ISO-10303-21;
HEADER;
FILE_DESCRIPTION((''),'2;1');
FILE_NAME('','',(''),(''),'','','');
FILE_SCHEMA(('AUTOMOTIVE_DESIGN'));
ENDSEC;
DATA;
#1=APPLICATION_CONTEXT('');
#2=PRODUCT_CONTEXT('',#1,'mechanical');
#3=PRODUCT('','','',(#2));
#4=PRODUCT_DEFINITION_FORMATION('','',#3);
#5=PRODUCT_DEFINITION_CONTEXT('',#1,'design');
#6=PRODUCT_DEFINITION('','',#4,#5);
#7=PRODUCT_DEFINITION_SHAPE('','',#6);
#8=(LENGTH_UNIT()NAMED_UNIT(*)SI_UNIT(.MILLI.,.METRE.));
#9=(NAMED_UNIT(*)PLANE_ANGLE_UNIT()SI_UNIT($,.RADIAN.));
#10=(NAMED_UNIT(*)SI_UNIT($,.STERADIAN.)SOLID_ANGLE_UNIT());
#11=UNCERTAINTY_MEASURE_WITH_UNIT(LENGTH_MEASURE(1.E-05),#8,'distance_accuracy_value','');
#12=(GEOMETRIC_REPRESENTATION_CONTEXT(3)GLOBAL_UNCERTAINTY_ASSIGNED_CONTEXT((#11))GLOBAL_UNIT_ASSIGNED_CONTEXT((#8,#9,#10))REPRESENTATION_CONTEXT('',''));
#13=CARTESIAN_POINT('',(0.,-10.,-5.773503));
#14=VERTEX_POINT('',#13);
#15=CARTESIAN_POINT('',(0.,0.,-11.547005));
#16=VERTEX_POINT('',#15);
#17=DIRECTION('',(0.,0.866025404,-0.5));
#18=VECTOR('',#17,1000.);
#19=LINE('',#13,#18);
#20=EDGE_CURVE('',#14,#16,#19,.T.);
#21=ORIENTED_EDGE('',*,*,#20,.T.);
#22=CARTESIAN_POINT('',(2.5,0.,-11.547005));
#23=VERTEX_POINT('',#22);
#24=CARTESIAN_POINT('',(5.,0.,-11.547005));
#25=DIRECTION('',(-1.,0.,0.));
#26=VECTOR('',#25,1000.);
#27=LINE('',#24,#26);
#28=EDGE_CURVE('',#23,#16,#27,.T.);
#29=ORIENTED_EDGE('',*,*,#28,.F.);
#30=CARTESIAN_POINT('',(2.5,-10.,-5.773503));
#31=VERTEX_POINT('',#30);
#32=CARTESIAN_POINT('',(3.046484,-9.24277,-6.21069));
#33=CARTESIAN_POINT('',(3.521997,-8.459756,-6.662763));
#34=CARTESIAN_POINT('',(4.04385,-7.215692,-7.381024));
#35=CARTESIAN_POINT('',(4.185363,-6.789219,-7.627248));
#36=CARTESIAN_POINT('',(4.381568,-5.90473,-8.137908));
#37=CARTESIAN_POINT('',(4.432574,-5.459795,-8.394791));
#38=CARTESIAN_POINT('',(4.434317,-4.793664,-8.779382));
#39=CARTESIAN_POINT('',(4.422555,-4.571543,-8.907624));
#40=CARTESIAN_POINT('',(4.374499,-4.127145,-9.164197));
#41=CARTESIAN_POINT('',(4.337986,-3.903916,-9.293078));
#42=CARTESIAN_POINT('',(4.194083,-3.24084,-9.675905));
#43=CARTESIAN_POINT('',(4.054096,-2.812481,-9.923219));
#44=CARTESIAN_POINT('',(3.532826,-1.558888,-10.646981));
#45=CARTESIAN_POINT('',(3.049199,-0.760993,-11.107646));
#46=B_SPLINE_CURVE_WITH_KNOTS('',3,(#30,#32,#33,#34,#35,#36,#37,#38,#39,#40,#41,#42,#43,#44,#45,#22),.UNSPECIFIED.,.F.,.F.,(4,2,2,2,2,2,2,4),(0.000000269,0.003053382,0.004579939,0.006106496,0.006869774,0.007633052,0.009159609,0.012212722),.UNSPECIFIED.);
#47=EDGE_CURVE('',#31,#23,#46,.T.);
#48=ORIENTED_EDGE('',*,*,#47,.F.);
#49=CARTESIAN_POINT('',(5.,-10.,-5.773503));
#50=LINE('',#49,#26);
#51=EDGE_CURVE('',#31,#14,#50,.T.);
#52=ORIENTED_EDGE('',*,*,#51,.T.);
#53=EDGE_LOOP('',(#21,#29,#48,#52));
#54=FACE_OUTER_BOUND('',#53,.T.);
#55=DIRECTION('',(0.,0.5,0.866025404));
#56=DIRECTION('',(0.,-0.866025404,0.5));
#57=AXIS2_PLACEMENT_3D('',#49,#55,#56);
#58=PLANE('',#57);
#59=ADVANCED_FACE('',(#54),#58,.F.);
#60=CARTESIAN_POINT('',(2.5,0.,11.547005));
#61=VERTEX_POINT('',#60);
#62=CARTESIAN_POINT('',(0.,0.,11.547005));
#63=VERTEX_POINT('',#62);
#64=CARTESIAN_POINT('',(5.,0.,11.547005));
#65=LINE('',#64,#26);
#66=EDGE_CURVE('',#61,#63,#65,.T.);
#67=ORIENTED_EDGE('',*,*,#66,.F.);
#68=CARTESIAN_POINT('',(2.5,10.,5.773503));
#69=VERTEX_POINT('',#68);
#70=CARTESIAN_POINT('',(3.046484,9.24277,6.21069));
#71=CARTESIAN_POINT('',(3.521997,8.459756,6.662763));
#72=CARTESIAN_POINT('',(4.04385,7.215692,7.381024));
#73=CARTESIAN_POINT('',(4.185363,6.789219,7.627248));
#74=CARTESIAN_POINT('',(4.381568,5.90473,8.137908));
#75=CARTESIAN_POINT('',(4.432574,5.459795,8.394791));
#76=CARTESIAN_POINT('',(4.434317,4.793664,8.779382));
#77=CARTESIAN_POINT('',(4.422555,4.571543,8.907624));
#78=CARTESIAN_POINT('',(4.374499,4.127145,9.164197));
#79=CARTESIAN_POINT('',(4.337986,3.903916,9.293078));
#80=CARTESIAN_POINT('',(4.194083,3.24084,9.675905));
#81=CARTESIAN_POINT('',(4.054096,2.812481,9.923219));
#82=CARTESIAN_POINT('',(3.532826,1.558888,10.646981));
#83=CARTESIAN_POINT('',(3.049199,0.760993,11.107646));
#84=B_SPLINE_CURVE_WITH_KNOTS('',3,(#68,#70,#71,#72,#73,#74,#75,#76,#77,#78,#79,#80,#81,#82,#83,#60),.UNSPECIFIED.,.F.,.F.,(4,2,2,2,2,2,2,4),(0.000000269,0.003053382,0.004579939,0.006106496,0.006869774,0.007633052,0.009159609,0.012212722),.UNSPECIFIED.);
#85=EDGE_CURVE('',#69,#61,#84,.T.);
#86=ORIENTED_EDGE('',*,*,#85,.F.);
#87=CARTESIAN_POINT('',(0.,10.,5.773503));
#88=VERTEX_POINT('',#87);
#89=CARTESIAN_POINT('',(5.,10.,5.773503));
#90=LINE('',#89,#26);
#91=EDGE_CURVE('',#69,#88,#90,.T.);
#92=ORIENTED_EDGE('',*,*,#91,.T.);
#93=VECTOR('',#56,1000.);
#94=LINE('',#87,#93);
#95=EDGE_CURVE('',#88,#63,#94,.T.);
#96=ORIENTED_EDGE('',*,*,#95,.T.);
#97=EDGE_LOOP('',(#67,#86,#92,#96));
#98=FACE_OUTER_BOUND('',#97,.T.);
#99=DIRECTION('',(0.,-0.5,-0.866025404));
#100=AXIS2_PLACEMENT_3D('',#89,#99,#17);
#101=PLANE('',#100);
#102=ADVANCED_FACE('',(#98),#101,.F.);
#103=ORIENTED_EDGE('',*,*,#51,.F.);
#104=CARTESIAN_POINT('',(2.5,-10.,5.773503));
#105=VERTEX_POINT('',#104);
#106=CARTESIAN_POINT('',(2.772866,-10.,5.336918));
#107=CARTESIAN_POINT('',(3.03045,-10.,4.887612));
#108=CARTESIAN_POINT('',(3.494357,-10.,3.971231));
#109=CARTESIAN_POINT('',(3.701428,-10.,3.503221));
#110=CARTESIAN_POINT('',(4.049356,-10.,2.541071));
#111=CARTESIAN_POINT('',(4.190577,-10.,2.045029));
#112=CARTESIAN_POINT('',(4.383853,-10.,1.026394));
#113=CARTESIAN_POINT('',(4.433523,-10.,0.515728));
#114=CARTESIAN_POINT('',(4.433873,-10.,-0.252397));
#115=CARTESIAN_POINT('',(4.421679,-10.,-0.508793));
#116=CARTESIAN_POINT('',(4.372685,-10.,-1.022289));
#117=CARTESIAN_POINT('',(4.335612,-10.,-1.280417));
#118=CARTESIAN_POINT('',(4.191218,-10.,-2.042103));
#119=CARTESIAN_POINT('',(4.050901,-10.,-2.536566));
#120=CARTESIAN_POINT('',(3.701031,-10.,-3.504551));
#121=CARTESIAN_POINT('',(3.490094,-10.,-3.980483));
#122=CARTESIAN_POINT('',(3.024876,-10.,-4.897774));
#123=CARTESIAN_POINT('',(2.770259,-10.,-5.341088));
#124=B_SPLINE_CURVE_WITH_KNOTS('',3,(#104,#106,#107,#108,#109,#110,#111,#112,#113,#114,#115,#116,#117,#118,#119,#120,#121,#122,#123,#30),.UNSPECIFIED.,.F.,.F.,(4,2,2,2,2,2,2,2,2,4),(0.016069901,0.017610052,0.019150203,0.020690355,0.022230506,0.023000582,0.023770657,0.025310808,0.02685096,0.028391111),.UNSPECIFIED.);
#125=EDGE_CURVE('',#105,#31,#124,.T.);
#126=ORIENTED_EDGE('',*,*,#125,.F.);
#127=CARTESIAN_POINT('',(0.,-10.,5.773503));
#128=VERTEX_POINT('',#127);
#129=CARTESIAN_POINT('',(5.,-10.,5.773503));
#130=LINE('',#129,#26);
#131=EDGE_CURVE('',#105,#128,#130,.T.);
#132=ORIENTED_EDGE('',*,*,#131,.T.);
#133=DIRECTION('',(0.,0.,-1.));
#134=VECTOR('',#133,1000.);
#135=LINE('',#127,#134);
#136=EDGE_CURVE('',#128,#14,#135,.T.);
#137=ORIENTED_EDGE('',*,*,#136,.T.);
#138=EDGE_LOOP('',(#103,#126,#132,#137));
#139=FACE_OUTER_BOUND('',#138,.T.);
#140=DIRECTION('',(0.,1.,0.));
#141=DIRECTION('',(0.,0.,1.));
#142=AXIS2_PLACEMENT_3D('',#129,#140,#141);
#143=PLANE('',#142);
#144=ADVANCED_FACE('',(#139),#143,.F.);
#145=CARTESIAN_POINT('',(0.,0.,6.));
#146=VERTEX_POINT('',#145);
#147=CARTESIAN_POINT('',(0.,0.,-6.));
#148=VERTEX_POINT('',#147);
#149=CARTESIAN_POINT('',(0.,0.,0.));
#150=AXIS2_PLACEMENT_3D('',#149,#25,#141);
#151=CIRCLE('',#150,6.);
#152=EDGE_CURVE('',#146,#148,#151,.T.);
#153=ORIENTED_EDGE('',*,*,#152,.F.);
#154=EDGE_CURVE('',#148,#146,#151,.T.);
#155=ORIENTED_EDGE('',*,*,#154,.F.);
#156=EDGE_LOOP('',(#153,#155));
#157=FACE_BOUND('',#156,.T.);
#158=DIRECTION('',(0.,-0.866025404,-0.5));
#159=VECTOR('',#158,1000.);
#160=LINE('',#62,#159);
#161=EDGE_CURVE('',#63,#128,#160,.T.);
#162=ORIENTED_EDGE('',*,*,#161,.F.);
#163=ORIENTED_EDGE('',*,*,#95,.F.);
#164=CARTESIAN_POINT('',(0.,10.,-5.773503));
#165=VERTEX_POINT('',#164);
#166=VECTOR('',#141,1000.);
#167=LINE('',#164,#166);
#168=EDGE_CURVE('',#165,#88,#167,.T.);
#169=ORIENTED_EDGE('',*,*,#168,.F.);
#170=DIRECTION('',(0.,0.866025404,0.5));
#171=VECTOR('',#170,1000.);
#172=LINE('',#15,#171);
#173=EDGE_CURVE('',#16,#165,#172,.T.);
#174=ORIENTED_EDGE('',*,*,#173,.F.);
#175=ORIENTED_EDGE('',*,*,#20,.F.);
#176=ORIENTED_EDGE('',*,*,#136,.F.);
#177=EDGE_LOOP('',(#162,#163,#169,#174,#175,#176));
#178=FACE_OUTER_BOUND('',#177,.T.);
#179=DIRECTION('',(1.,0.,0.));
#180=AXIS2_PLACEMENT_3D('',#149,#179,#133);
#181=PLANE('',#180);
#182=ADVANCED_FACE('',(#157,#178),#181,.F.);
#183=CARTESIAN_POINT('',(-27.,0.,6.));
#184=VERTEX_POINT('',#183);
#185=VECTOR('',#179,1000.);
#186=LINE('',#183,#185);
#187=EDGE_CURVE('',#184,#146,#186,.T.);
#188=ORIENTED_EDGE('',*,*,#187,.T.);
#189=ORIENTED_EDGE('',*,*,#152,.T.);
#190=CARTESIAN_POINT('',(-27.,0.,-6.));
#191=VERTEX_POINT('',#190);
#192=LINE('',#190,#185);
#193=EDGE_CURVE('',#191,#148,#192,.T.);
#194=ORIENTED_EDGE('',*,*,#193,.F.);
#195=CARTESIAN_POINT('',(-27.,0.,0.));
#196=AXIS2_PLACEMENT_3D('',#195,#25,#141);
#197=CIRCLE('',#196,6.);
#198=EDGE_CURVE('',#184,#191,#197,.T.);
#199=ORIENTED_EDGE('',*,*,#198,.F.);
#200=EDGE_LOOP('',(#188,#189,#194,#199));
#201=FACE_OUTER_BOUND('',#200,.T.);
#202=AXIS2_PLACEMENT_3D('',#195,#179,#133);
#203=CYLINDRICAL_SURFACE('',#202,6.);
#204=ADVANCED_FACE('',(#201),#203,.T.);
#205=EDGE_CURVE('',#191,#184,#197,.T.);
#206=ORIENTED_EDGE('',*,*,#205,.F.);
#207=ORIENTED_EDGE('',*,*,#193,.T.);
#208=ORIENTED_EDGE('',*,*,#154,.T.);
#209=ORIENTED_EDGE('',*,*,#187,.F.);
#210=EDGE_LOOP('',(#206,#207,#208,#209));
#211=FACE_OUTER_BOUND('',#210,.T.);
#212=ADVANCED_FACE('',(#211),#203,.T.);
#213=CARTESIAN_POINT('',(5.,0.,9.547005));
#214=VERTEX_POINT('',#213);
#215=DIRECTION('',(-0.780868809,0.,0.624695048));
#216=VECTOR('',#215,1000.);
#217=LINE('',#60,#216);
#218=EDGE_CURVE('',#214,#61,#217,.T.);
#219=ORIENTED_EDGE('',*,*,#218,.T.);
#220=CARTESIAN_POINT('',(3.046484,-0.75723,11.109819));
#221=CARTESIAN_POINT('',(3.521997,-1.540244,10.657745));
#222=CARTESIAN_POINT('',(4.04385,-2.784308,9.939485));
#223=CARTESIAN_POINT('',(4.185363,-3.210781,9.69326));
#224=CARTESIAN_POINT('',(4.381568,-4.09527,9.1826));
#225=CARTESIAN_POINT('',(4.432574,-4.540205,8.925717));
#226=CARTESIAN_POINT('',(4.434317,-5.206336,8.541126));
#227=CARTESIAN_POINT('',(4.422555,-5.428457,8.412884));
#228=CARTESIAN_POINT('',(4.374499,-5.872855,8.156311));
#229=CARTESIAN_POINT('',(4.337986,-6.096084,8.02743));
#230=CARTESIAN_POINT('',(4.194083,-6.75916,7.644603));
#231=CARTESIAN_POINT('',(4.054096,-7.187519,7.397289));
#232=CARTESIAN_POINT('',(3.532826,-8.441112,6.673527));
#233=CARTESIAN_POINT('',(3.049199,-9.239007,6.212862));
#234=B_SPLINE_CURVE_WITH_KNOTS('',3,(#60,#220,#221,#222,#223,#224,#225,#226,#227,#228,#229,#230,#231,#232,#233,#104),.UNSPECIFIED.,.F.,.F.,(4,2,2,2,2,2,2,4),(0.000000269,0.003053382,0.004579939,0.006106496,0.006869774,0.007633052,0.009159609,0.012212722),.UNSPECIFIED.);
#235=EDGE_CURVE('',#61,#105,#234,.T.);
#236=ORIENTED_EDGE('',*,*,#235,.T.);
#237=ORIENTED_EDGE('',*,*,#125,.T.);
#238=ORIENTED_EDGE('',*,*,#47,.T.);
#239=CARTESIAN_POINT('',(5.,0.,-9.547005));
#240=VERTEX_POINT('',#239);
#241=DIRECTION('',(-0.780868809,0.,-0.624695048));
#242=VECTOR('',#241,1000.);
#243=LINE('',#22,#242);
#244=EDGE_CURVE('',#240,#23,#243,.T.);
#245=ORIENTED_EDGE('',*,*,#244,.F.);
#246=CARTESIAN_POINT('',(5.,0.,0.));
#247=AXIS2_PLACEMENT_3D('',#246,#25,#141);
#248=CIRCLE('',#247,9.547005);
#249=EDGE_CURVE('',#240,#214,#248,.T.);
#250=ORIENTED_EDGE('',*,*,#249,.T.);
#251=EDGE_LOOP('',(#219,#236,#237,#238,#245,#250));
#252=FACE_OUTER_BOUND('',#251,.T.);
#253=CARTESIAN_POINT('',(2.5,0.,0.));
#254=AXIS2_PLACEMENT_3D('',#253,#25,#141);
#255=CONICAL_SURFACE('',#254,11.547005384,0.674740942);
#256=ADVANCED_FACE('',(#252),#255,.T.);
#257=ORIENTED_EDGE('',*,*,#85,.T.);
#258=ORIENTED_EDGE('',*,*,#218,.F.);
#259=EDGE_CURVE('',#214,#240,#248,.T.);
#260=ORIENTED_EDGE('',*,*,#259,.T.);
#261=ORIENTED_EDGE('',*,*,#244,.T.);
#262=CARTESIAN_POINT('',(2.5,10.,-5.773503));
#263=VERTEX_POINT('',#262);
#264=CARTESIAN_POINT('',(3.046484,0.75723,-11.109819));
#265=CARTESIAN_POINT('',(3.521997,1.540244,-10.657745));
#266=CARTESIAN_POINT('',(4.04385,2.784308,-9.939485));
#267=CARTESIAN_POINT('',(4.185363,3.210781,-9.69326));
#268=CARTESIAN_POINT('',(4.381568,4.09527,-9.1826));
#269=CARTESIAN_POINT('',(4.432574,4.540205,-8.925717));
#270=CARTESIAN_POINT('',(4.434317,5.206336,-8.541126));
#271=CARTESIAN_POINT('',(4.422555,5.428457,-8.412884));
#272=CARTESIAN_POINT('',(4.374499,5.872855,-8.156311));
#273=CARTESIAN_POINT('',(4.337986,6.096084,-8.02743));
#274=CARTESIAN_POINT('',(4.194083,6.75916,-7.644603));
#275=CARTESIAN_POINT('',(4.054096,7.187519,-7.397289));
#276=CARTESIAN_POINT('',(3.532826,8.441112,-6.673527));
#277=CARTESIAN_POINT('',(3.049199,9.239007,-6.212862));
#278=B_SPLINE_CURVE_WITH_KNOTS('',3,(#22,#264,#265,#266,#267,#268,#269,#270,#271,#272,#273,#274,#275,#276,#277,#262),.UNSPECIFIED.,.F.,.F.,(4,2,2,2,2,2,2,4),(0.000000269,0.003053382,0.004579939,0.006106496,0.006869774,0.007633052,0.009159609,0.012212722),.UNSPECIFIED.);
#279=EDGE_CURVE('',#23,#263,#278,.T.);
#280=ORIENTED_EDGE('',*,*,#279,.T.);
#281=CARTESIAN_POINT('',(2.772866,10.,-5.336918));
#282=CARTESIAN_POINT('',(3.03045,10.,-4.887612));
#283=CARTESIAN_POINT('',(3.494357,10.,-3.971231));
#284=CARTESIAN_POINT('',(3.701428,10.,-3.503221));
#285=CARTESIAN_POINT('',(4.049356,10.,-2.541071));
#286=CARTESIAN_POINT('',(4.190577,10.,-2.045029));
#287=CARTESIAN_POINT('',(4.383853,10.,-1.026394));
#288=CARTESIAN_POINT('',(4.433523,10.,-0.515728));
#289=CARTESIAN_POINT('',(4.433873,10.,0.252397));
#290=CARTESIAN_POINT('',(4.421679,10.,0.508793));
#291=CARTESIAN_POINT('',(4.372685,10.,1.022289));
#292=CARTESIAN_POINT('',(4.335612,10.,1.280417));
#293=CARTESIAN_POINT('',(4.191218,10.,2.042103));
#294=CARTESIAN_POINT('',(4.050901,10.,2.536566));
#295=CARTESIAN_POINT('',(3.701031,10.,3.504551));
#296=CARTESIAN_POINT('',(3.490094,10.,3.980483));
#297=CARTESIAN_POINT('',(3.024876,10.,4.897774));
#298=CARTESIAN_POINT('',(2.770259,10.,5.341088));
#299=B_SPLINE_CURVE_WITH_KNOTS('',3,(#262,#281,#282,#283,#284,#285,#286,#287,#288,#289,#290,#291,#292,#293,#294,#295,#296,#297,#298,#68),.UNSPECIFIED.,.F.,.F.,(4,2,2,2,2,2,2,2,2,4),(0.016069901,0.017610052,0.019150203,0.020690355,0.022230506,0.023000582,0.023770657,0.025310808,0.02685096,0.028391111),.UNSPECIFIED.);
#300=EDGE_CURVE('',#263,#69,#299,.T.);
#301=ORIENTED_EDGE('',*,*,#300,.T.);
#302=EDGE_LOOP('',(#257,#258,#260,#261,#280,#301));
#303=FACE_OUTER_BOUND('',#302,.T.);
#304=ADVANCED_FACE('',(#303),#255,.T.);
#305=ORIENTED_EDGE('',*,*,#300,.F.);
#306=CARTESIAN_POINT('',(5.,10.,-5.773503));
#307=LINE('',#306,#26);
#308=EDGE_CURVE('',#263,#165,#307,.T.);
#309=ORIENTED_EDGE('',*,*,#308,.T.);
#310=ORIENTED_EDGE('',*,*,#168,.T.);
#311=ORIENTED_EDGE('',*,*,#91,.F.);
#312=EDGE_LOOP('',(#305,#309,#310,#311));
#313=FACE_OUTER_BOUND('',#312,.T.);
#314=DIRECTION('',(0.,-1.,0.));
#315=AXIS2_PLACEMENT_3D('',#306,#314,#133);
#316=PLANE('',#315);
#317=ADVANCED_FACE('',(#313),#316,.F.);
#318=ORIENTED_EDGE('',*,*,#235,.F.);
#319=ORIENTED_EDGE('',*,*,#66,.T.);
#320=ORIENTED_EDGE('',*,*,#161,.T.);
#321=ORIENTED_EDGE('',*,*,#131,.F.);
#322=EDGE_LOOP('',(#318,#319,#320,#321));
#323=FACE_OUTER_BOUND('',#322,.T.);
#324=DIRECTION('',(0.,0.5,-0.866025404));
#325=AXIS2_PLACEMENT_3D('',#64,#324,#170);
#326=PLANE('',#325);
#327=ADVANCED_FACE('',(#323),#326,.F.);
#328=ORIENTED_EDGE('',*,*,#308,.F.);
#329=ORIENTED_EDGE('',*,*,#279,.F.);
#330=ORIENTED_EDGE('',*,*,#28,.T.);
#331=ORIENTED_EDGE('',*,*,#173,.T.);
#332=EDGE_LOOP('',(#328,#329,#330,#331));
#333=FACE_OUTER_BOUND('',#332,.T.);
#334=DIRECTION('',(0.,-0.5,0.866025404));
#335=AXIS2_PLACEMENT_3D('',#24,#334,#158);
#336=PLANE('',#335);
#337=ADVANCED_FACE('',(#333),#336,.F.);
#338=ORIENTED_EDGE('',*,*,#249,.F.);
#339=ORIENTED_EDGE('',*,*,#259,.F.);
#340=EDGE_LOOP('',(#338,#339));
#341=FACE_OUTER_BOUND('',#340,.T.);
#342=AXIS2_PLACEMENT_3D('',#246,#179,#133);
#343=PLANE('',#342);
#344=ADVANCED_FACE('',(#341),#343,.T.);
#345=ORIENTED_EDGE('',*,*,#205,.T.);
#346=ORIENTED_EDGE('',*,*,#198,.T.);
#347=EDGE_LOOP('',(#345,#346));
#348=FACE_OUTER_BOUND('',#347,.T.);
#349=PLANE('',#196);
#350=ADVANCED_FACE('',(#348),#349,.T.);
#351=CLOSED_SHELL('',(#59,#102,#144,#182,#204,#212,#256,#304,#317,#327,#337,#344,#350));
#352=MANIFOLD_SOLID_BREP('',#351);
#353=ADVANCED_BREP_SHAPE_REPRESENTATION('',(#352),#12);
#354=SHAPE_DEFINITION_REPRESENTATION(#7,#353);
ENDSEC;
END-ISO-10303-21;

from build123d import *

# Parameters (mm, degrees)
HEX_HEAD_DEPTH     = 5
SHANK_PROFILE_12_R = 6
SHANK_12_DEPTH     = 27


with BuildPart() as part:
    # Hex Head Profile 20AF → Hex Head (new body)
    with BuildSketch(Plane(origin=(0, 0, 0), x_dir=(0, 0, -1), z_dir=(1, 0, 0))):
        Polygon((11.547005384, 0), (5.773502692, 10), (-5.773502692, 10), (-11.547005384, 0), (-5.773502692, -10), (5.773502692, -10), align=None)
    extrude(amount=HEX_HEAD_DEPTH)

    # Shank Profile Ø12 → Shank Ø12 (add)
    with BuildSketch(Plane.ZY):
        Circle(SHANK_PROFILE_12_R)
    extrude(amount=SHANK_12_DEPTH)

    # Head Chamfer Profile → Head Chamfer (revolve, cut)
    with BuildSketch(Plane(origin=(0, 0, 0), x_dir=(1, 0, 0), z_dir=(0, 1, 0)), mode=Mode.PRIVATE) as head_chamfer_sk:
        Polygon((2.5, 11.547005384), (5, 9.547005384), (5, 11.547005384), align=None)
    revolve(head_chamfer_sk.sketch.rotate(Axis((0, 0, 0), (1, 0, 0)), 180), axis=Axis((0, 0, 0), (1, 0, 0)), mode=Mode.SUBTRACT)


solid = part.part
